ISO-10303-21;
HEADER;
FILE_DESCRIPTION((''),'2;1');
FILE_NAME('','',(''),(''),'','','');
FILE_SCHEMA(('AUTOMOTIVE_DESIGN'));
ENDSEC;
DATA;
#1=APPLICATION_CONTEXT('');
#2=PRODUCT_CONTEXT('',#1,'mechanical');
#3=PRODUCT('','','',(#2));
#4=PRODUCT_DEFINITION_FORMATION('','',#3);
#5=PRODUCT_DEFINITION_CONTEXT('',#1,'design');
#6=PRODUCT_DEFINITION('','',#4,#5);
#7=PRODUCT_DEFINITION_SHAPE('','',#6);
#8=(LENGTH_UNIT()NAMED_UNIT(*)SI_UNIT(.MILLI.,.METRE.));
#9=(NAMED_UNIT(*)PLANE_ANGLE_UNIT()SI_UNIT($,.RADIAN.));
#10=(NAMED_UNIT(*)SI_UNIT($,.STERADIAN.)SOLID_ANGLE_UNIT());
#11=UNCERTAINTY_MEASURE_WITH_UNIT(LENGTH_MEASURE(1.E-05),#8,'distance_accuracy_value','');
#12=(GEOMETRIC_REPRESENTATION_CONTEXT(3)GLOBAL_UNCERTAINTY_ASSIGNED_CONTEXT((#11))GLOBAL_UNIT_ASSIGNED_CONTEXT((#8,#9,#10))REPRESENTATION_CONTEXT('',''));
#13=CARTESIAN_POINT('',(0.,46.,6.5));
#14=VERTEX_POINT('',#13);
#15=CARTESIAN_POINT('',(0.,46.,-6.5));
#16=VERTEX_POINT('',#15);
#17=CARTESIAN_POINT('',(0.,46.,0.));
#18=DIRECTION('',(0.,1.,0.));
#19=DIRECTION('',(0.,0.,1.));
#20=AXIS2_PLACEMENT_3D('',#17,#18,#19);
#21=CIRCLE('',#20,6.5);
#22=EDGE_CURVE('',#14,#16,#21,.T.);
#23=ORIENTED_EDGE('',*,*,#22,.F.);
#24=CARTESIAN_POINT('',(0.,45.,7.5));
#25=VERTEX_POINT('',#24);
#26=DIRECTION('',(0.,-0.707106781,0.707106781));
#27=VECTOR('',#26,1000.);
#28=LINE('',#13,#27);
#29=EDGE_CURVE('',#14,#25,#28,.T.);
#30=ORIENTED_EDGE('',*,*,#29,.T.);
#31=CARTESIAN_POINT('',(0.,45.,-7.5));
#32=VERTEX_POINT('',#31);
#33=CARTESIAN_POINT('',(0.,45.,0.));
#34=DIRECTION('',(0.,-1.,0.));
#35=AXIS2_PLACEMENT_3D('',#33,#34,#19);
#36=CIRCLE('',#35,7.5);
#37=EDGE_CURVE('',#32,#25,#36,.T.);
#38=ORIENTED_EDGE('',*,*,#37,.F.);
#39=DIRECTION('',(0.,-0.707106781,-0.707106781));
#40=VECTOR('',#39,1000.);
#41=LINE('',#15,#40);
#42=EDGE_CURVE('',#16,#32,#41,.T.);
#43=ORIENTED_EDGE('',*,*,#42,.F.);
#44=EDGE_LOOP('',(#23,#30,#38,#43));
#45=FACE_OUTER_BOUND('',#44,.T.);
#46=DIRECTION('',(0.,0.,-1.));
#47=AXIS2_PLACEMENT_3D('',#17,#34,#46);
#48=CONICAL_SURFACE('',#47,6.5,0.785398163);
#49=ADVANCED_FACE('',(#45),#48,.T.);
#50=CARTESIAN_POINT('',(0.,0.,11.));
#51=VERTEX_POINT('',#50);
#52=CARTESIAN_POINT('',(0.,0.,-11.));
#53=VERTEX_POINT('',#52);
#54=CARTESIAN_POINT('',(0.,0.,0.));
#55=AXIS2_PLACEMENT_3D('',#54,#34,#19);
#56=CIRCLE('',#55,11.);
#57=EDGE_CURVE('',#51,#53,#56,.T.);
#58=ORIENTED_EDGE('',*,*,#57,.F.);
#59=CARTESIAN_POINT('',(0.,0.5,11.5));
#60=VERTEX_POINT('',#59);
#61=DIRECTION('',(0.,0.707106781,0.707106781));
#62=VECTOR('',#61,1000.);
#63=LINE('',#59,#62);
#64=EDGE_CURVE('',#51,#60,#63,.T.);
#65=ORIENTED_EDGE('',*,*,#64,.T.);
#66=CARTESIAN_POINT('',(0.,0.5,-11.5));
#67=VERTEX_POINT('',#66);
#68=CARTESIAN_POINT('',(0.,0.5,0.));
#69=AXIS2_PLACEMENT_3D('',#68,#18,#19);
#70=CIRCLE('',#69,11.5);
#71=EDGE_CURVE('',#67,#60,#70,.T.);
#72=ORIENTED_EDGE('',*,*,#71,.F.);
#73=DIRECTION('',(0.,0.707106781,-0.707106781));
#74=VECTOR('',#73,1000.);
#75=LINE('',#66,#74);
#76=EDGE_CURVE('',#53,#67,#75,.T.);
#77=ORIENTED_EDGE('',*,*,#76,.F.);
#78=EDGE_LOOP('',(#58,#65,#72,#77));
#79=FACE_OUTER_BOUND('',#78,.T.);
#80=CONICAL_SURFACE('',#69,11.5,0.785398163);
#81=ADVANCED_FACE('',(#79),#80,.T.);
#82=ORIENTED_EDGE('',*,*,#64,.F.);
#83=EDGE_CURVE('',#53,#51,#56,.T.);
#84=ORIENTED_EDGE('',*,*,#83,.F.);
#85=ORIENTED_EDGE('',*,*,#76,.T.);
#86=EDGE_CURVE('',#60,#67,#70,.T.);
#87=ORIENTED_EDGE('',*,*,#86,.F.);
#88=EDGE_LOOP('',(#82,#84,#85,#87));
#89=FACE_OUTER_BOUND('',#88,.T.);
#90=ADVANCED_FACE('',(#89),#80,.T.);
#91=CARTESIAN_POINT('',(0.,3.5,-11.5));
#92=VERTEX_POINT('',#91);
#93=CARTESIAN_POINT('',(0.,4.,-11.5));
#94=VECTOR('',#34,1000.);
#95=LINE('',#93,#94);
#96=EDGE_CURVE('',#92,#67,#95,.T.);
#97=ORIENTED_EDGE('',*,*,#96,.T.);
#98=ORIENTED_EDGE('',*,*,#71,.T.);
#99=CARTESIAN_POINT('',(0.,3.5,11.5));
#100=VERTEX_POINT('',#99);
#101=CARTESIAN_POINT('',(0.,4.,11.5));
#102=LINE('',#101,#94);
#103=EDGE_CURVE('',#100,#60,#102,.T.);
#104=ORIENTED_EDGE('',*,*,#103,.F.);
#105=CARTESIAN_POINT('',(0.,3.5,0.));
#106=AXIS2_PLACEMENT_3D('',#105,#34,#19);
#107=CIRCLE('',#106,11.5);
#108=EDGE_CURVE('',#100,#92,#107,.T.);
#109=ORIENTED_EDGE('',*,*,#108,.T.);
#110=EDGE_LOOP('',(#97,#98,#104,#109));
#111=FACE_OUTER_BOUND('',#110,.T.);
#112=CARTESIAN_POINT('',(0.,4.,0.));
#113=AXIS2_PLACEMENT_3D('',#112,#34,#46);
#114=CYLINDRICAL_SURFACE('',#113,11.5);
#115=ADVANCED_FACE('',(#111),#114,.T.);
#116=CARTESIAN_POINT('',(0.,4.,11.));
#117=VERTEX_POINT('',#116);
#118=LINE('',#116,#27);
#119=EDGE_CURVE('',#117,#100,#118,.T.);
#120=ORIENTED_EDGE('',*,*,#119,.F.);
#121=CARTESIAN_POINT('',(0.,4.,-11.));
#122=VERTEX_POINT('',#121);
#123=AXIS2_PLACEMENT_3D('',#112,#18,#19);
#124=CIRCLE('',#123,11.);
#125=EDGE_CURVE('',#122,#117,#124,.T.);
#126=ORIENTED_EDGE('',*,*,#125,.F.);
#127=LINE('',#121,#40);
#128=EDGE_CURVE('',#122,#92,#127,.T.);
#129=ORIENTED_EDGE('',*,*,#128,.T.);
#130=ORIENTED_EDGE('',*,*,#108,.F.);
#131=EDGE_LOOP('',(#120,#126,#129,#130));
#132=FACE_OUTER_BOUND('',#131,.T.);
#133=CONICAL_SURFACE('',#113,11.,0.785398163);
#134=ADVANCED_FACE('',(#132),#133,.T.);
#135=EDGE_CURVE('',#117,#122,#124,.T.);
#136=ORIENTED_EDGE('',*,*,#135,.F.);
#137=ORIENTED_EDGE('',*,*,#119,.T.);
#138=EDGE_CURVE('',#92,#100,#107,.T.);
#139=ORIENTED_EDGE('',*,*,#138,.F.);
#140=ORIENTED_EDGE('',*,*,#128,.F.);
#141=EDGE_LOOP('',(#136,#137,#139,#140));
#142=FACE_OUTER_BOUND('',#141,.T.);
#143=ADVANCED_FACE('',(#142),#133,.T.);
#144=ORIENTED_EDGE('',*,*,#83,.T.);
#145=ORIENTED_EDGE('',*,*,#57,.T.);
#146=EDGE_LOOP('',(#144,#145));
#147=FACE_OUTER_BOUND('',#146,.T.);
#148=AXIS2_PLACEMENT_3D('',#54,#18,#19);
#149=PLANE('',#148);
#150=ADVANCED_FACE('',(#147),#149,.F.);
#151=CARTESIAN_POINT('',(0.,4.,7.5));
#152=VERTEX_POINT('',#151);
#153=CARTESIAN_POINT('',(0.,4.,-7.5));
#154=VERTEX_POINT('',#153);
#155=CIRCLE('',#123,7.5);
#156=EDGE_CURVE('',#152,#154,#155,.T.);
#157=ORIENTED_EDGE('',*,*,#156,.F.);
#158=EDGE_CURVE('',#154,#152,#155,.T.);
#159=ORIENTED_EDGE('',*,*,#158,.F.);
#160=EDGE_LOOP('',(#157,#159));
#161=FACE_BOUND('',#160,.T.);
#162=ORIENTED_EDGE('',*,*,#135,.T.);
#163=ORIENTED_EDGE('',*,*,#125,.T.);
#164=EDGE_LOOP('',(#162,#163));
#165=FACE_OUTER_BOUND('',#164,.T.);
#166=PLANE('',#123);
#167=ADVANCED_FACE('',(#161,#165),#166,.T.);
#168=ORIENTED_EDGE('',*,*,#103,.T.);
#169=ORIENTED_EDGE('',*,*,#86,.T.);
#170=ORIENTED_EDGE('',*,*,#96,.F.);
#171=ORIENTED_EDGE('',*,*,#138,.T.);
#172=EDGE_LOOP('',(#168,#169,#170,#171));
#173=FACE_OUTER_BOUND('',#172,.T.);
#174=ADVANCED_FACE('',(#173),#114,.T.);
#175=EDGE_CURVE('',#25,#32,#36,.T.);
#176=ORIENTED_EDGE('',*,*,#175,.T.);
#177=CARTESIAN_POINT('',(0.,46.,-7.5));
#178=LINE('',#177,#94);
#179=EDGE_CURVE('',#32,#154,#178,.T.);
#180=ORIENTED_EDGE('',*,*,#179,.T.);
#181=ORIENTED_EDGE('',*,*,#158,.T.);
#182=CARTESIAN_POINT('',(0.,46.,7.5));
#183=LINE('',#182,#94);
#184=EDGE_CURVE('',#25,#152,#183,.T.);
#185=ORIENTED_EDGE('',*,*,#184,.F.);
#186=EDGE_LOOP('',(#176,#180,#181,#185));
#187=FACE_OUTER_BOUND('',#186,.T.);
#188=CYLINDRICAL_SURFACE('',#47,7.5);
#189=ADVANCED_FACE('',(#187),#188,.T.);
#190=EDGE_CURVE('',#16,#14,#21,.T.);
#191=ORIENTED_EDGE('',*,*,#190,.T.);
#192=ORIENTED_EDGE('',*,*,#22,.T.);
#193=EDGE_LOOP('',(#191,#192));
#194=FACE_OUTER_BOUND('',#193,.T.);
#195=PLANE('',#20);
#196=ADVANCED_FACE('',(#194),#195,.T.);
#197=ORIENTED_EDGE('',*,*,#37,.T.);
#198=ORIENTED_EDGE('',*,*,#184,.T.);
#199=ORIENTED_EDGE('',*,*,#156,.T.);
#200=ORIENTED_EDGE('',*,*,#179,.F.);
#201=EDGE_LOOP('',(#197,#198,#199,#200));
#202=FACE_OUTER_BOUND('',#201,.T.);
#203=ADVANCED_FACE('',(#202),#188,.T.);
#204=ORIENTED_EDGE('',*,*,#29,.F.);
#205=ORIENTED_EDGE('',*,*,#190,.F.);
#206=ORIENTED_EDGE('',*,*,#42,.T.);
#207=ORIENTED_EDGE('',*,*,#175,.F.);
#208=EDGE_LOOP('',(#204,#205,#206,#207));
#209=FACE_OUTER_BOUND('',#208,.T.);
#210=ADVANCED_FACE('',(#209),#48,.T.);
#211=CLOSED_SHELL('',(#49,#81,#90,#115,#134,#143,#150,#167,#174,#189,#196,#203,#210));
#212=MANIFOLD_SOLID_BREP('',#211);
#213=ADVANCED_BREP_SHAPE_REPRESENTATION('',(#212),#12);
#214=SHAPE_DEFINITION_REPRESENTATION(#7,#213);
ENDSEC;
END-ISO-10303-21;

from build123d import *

# Parameters (mm, degrees)
SKETCH1_R           = 11.5
BOSS_EXTRUDE1_DEPTH = 4
SKETCH2_R           = 7.5
BOSS_EXTRUDE2_DEPTH = 42
CHAMFER1_SIZE       = 1
CHAMFER2_SIZE       = 0.5


with BuildPart() as part:
    # Sketch1 → Boss-Extrude1 (new body)
    with BuildSketch(Plane(origin=(0, 0, 0), x_dir=(1, 0, 0), z_dir=(0, 1, 0))):
        with Locations(Location((0, 0, 0), (0, 0, 270))):
            Circle(SKETCH1_R)
    extrude(amount=BOSS_EXTRUDE1_DEPTH)

    # Sketch2 → Boss-Extrude2 (add)
    with BuildSketch(Plane(origin=(0, 4, 0), x_dir=(1, 0, 0), z_dir=(0, 1, 0))):
        with Locations(Location((0, 0, 0), (0, 0, 90))):
            Circle(SKETCH2_R)
    extrude(amount=BOSS_EXTRUDE2_DEPTH)

    # Chamfer1
    chamfer1_edges = [part.edges().sort_by_distance(p)[0] for p in [
        (0, 46, 7.5),
    ]]
    chamfer(chamfer1_edges, length=CHAMFER1_SIZE)

    # Chamfer2
    chamfer2_edges = [part.edges().sort_by_distance(p)[0] for p in [
        (0, 0, -11.5),
        (0, 4, -11.5),
    ]]
    chamfer(chamfer2_edges, length=CHAMFER2_SIZE)


solid = part.part
